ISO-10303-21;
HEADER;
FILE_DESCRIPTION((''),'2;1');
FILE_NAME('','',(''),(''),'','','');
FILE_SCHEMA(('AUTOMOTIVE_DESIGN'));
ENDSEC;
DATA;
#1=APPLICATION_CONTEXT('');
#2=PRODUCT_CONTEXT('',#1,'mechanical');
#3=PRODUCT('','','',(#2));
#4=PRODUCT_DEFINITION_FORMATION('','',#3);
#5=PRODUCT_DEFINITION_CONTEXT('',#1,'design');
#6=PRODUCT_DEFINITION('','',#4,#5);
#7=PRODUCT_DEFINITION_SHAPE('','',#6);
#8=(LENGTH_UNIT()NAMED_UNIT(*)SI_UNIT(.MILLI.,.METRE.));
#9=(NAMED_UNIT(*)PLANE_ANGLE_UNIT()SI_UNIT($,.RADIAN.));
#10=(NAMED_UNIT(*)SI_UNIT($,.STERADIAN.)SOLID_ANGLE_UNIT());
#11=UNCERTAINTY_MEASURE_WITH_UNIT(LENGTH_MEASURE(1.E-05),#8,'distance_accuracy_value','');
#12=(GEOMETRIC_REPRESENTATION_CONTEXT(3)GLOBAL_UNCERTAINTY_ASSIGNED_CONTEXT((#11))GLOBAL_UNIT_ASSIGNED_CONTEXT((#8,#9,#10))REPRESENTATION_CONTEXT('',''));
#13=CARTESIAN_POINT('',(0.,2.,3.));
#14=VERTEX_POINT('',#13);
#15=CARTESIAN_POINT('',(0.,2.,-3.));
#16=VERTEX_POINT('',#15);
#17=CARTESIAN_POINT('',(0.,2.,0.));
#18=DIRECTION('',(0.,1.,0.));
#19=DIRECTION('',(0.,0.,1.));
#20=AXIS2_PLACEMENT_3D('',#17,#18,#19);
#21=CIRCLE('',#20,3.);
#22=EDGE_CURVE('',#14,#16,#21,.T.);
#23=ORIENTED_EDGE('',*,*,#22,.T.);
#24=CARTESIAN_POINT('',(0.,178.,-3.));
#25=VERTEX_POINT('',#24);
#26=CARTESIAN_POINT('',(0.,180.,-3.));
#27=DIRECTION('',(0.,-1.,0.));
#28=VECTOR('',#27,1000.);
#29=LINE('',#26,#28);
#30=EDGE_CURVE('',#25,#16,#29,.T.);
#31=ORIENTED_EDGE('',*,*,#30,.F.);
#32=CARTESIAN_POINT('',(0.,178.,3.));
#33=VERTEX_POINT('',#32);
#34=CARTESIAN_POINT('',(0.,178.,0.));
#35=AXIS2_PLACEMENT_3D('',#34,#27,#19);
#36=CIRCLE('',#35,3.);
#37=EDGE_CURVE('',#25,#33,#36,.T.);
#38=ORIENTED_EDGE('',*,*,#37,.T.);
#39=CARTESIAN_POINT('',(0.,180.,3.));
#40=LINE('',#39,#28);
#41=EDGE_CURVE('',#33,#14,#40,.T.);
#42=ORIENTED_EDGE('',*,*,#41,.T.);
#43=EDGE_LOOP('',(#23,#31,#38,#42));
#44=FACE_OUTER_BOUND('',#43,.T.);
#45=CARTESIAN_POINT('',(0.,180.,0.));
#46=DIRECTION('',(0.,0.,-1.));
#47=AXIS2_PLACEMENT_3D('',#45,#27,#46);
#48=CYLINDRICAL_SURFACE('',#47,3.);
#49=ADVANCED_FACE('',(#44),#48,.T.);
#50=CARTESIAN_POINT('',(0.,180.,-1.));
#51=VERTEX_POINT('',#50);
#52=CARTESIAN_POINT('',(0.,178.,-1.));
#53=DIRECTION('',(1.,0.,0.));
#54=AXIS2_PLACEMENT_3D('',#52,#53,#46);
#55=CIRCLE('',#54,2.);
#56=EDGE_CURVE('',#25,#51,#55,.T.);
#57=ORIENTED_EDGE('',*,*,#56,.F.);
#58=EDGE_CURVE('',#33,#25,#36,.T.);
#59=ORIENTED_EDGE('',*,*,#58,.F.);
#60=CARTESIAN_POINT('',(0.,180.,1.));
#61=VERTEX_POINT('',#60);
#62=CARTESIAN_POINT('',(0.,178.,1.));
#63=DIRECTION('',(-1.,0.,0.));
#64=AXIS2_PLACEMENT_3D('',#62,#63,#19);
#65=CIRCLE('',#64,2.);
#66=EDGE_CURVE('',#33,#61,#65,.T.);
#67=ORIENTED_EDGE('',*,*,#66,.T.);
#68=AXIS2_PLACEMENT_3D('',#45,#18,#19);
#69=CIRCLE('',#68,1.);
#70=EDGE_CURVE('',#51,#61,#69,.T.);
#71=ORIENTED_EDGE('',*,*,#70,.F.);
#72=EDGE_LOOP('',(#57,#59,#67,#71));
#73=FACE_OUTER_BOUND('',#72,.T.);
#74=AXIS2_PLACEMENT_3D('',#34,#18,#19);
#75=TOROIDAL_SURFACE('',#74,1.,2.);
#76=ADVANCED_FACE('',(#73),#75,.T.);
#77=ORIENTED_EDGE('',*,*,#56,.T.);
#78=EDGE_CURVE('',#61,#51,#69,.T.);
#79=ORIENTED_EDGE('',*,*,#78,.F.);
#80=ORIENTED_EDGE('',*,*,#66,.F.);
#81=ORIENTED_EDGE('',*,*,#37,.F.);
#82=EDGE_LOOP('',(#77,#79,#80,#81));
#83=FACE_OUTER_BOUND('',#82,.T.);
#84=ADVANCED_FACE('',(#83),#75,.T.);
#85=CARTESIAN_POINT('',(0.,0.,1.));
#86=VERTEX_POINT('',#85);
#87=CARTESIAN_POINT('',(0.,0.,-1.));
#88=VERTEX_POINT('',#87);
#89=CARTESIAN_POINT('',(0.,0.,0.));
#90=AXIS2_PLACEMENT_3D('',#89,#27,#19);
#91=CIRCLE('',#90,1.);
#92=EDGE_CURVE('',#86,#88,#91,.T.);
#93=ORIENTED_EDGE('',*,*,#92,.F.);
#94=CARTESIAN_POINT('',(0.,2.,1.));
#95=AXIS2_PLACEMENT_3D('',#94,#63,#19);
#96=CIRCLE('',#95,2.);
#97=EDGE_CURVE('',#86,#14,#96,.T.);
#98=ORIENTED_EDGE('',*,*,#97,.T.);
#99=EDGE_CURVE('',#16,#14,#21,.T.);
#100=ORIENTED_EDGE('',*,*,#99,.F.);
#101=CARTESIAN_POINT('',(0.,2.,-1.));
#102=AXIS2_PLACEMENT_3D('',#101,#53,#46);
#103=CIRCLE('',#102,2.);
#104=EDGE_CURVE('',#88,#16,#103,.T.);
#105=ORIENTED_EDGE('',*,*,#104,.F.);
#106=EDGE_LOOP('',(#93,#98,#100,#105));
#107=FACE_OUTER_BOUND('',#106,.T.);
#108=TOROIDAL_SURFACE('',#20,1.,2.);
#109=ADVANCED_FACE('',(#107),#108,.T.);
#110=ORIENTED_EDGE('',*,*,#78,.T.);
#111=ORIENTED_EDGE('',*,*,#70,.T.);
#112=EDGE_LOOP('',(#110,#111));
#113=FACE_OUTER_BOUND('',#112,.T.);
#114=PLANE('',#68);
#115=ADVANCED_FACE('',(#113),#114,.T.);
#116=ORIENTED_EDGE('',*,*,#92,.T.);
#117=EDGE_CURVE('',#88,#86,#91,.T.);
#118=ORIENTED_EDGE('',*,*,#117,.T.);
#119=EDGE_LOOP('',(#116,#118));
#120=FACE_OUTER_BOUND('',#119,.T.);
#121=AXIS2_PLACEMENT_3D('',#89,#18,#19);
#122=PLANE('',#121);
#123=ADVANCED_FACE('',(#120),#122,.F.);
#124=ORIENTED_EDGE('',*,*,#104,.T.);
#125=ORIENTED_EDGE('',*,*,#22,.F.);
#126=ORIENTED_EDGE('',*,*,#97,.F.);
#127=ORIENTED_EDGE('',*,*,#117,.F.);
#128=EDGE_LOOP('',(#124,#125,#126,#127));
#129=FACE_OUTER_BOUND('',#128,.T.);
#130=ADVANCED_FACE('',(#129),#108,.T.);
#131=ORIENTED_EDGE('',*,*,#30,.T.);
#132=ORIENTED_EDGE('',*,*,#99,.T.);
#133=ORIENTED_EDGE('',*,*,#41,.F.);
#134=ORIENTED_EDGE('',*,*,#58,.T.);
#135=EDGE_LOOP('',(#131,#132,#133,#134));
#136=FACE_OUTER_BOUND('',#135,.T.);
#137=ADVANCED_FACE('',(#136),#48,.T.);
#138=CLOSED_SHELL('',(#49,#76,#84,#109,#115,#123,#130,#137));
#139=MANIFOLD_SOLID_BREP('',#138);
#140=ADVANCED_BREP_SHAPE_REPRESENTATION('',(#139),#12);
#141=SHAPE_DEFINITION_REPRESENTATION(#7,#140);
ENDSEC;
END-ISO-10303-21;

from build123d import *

# Parameters (mm, degrees)
SKETCH1_R           = 3
BOSS_EXTRUDE1_DEPTH = 180
FILLET1_R           = 2


with BuildPart() as part:
    # Sketch1 → Boss-Extrude1 (new body)
    with BuildSketch(Plane(origin=(0, 0, 0), x_dir=(1, 0, 0), z_dir=(0, 1, 0))):
        with Locations(Location((0, 0, 0), (0, 0, 90))):
            Circle(SKETCH1_R)
    extrude(amount=BOSS_EXTRUDE1_DEPTH)

    # Fillet1
    fillet1_edges = [part.edges().sort_by_distance(p)[0] for p in [
        (0, 0, 3),
        (0, 180, 3),
    ]]
    fillet(fillet1_edges, radius=FILLET1_R)


solid = part.part
